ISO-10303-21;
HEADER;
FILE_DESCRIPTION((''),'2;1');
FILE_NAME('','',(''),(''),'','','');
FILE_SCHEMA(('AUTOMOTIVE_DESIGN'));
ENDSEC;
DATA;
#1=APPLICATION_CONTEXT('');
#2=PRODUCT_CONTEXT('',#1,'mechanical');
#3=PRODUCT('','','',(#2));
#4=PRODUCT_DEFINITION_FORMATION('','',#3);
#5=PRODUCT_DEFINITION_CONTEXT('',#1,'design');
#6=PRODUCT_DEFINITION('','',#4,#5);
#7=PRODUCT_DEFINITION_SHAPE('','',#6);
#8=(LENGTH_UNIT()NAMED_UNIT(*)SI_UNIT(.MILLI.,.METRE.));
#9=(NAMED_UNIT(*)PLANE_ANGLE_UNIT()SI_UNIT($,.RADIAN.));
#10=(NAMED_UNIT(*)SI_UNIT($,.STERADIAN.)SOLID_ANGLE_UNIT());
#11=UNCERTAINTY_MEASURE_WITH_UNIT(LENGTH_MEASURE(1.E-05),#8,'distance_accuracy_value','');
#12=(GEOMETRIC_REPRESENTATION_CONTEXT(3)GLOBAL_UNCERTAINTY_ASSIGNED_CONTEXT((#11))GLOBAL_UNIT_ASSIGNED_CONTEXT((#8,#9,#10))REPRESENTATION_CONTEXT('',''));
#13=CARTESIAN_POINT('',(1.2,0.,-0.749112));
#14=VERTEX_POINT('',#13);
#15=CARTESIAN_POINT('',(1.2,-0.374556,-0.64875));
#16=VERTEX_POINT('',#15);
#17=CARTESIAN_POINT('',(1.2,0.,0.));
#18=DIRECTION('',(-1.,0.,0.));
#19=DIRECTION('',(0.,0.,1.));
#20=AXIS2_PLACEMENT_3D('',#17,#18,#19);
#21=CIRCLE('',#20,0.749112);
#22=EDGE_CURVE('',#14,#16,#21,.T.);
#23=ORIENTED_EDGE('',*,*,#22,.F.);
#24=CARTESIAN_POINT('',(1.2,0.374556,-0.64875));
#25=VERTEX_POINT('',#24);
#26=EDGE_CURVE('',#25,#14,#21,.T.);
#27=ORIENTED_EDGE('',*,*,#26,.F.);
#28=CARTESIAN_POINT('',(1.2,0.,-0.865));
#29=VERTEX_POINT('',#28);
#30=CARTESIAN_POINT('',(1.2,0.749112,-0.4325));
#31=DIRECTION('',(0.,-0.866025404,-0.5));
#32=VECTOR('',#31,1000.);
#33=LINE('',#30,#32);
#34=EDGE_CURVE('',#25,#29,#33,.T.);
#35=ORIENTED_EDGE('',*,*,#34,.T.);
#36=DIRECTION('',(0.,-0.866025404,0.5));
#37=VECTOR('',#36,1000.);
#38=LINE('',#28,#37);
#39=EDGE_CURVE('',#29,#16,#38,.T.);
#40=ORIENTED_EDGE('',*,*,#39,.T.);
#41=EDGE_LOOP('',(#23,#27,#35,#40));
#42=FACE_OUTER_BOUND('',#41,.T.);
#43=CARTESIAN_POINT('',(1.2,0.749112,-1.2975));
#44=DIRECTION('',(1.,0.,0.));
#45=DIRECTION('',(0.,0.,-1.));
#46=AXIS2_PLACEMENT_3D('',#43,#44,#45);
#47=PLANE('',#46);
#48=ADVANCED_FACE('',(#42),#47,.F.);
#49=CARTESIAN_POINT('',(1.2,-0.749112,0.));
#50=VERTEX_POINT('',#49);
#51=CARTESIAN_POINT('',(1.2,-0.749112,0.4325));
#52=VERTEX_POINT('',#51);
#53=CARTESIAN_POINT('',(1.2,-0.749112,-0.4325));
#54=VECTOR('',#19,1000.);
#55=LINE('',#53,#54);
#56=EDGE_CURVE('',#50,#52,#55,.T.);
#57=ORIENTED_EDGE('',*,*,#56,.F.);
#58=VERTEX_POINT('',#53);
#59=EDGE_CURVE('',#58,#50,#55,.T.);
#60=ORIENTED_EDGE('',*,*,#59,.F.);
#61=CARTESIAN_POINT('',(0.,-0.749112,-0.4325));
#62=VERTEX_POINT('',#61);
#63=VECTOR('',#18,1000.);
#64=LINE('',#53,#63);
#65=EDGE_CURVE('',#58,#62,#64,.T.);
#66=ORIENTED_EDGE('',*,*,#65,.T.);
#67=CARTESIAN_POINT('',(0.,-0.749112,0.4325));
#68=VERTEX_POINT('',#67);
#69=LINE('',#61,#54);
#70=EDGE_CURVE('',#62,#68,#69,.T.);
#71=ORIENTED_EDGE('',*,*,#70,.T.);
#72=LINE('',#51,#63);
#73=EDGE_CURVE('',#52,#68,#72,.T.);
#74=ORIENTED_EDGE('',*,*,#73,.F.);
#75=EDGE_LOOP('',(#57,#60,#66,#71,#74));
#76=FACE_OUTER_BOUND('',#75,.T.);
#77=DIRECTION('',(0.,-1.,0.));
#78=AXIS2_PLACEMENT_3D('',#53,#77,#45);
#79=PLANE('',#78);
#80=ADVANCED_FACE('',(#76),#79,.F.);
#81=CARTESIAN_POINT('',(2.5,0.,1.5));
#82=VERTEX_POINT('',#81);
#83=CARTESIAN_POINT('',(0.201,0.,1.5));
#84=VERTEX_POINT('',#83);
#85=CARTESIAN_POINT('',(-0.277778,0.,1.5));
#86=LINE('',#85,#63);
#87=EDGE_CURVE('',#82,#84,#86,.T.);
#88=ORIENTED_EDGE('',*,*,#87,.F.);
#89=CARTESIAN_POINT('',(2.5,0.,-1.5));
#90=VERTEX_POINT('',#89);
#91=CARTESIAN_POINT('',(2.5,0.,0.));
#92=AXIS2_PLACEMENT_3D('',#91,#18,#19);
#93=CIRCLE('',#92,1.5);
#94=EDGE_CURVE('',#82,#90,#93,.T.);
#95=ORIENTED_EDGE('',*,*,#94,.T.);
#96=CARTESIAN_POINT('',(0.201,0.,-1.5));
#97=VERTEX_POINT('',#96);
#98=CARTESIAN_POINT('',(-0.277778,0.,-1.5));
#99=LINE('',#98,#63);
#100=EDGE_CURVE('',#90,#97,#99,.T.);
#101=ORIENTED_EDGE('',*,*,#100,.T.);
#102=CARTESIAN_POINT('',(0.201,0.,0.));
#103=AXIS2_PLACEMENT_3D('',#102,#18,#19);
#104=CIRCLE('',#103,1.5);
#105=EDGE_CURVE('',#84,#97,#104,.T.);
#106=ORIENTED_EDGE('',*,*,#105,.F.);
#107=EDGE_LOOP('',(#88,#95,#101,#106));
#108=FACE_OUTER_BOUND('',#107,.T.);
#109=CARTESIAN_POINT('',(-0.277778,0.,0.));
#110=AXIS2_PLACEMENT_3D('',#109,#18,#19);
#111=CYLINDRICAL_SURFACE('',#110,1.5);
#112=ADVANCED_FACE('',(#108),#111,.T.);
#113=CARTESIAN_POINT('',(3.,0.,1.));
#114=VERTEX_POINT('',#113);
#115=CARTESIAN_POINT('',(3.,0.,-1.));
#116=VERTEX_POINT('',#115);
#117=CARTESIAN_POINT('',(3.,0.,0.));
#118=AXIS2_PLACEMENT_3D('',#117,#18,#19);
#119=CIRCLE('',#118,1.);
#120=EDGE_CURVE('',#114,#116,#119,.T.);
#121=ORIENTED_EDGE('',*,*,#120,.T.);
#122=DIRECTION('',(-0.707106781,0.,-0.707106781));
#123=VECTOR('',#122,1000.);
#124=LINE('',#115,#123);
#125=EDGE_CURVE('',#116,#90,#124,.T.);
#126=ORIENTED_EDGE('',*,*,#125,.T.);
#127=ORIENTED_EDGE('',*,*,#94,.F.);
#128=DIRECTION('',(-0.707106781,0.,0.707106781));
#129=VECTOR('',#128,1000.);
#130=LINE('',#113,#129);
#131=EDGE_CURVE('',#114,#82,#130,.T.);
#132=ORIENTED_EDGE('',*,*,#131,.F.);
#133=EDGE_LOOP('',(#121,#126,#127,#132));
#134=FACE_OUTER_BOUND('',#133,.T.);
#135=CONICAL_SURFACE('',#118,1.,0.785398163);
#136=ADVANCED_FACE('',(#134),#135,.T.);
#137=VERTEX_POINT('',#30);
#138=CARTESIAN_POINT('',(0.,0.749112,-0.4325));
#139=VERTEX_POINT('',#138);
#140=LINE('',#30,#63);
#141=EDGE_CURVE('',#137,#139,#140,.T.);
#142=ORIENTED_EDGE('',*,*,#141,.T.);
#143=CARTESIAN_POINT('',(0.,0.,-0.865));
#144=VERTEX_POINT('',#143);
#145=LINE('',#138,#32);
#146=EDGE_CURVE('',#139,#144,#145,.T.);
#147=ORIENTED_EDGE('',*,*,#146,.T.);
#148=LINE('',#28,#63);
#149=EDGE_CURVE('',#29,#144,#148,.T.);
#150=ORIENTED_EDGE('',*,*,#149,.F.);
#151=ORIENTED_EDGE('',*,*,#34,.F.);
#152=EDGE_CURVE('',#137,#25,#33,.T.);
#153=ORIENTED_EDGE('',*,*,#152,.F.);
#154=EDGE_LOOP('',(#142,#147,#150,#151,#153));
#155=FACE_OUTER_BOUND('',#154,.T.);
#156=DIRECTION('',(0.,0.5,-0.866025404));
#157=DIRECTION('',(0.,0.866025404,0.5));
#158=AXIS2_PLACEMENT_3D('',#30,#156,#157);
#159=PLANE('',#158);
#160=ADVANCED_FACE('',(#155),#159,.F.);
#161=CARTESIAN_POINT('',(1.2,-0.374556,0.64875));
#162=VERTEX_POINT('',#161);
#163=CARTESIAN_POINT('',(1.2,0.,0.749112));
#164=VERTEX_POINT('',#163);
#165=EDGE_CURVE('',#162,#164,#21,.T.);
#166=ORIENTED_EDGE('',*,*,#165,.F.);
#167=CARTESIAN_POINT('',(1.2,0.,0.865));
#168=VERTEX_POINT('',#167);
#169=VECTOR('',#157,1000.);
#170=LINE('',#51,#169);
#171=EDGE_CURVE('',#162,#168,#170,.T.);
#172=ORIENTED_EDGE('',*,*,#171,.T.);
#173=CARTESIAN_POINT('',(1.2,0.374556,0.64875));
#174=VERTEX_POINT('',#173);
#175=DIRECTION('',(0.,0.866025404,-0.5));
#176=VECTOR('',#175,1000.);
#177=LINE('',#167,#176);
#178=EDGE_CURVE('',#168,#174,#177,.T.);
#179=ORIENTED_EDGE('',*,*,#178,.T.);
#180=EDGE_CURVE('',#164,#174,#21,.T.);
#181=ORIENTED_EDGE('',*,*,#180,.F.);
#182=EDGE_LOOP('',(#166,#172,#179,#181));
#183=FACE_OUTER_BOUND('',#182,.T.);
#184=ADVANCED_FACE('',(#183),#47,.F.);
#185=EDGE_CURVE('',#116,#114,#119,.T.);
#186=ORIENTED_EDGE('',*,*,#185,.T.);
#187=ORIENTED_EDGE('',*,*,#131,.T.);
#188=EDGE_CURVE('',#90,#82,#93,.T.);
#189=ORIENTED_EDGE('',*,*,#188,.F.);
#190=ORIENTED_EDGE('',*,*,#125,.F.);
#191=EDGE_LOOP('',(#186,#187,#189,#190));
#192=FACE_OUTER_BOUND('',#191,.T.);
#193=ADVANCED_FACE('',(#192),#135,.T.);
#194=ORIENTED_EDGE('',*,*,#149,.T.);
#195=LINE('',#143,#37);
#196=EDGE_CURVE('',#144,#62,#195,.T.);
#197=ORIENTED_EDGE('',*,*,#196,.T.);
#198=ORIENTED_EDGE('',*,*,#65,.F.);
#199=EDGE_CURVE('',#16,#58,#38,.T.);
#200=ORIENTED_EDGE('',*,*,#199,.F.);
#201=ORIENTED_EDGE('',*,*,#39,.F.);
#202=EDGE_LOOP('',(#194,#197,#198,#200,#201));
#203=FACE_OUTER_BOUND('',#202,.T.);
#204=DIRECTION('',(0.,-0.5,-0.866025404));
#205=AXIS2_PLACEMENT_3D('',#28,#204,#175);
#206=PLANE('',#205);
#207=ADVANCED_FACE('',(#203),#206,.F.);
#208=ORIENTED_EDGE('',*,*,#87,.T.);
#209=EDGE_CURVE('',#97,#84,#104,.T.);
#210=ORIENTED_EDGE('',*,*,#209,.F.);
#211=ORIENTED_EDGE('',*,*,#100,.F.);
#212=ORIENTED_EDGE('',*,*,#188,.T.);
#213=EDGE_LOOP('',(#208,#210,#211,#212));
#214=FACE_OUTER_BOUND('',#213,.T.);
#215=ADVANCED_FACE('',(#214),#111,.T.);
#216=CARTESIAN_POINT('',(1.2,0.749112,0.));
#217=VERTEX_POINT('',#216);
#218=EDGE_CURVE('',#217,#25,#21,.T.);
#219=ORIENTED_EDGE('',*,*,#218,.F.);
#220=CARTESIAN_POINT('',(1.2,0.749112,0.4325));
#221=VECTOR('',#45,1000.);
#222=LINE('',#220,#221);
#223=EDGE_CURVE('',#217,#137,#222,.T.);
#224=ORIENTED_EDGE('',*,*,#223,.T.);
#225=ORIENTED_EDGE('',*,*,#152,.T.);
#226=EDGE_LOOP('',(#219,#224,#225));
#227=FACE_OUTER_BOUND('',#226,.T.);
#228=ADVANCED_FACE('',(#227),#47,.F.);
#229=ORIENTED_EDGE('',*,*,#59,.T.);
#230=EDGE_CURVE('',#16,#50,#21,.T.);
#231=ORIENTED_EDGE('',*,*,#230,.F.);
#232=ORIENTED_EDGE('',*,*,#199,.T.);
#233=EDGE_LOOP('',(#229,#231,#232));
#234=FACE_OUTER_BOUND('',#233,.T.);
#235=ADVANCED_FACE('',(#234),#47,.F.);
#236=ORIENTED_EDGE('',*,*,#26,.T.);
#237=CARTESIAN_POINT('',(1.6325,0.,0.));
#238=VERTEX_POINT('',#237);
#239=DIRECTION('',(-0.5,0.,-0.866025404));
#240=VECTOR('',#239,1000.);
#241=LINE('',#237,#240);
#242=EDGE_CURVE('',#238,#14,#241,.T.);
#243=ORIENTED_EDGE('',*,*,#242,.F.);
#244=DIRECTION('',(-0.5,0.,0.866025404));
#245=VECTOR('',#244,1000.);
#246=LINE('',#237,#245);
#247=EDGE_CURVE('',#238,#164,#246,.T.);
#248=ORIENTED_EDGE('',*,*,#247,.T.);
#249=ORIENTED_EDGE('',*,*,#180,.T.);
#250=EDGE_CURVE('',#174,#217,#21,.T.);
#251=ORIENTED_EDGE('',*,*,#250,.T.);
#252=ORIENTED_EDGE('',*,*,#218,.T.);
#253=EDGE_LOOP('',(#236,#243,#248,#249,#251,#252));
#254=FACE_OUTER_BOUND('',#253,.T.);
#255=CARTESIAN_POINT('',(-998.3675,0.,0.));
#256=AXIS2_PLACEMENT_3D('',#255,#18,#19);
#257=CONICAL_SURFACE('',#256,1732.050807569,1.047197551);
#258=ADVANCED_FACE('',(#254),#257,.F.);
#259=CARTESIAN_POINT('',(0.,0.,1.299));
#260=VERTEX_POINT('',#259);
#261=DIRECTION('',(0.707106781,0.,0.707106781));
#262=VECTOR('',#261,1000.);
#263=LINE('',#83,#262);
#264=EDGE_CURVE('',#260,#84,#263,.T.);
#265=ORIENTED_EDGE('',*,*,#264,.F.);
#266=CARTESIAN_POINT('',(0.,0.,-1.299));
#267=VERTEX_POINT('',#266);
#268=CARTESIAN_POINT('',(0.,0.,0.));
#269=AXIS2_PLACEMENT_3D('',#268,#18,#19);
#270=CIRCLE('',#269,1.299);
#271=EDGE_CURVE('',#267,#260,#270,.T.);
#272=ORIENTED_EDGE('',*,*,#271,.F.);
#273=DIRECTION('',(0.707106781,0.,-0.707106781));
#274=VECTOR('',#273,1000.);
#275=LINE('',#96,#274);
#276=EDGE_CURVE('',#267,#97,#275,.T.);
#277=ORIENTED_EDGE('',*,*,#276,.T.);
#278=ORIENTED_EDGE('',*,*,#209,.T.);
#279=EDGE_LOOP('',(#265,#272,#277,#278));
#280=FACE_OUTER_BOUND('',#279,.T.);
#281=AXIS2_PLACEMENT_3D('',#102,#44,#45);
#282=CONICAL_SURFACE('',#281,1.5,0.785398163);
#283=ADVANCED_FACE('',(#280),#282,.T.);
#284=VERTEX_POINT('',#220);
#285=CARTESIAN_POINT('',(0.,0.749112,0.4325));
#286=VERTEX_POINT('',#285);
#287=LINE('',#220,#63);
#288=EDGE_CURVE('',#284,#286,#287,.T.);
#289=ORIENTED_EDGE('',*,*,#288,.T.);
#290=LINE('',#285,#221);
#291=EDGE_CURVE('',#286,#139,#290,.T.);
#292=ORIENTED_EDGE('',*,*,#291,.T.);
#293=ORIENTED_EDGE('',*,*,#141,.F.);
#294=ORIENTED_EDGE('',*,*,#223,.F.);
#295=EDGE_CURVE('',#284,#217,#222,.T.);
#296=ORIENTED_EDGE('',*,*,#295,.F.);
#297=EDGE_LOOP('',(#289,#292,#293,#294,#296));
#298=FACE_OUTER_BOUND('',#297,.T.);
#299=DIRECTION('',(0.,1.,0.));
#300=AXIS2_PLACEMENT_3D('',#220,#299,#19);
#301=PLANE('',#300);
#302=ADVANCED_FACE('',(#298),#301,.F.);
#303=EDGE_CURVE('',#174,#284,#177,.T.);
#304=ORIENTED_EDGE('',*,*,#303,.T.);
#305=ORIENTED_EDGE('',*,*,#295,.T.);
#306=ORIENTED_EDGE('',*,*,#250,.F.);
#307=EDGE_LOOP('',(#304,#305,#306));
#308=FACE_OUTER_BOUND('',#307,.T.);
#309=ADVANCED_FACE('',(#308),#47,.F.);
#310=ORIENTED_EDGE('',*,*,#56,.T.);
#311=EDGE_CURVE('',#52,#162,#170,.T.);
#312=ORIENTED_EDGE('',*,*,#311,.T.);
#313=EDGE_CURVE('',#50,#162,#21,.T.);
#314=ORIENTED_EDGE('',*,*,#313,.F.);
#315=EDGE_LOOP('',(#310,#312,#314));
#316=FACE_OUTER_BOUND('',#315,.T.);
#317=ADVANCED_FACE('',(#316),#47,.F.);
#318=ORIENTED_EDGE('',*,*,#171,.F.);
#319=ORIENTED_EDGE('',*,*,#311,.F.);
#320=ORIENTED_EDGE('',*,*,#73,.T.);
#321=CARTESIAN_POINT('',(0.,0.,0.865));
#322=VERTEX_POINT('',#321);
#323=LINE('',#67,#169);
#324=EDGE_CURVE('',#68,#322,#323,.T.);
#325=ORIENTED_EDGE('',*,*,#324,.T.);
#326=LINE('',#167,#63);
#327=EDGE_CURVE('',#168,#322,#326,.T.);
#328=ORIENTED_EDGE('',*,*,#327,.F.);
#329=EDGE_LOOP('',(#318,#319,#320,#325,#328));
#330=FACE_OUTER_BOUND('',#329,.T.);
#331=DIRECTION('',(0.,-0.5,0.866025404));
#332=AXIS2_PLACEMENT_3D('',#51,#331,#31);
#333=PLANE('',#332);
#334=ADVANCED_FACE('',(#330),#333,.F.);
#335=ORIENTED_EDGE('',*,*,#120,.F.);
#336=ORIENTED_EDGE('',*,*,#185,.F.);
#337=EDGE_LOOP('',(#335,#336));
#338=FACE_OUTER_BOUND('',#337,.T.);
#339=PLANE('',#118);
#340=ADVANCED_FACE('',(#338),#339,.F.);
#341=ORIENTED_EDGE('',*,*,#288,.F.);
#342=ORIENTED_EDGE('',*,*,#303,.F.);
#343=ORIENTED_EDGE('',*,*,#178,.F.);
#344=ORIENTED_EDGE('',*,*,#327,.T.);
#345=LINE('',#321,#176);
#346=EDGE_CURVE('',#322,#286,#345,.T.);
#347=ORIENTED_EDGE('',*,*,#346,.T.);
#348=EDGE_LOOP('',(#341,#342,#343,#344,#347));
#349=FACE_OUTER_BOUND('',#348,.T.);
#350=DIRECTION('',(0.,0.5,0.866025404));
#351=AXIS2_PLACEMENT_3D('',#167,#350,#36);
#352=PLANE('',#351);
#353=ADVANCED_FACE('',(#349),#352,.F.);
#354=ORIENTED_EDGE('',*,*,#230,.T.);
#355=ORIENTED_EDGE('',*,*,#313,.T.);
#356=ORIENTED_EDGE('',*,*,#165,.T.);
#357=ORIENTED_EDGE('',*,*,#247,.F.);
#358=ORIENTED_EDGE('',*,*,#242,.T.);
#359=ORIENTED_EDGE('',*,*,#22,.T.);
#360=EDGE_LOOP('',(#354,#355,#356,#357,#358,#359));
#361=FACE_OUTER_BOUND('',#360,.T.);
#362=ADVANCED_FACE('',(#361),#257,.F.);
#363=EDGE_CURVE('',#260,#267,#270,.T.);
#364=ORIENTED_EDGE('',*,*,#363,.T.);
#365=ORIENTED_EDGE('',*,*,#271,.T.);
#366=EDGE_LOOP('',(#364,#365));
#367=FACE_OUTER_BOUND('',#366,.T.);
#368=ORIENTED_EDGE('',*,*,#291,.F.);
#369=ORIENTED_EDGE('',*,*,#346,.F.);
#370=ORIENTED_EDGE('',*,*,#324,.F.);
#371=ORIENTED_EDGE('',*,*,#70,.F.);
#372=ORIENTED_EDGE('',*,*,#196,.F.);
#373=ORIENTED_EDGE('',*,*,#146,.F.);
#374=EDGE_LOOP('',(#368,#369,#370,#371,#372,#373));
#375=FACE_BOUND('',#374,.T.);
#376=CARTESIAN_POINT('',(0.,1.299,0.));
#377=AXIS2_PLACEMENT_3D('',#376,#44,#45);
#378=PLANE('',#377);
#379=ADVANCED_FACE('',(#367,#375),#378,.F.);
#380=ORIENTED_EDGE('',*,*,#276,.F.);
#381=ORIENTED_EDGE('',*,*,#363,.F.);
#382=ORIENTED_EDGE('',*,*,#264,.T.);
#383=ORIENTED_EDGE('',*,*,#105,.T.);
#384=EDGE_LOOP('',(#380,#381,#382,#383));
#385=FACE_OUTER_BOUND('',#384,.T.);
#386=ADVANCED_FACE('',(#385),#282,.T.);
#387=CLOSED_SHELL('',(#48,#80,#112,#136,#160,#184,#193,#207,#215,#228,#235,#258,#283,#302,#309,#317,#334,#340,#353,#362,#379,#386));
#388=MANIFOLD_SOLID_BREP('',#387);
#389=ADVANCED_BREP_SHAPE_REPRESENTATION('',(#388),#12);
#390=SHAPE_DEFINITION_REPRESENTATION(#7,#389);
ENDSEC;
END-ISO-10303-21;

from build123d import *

# Parameters (mm, degrees)
CUT_EXTRUDE1_DEPTH = 1.2


with BuildPart() as part:
    # Sketch1 → Base-Revolve (revolve)
    with BuildSketch(Plane.XY, mode=Mode.PRIVATE) as base_revolve_sk:
        Polygon((0, 0), (3, 0), (3, 1), (2.5, 1.5), (0.201, 1.5), (0, 1.299), align=None)
    revolve(base_revolve_sk.sketch.rotate(Axis((-0.277777778, 0, 0), (1, 0, 0)), 90), axis=Axis((-0.277777778, 0, 0), (1, 0, 0)))

    # Sketch2 → Cut-Extrude1 (cut)
    with BuildSketch(Plane.ZY):
        Polygon((-0.4325, -0.749111974), (0.4325, -0.749111974), (0.865, 0), (0.4325, 0.749111974), (-0.4325, 0.749111974), (-0.865, 0), align=None)
    extrude(amount=-CUT_EXTRUDE1_DEPTH, mode=Mode.SUBTRACT)

    # Sketch4 → Cut-Revolve2 (revolve, cut)
    with BuildSketch(Plane.XY, mode=Mode.PRIVATE) as cut_revolve2_sk:
        Polygon((1.2, 0.749111974), (1.6325, 0), (1.2, 0), align=None)
    revolve(cut_revolve2_sk.sketch.rotate(Axis((-0.277777778, 0, 0), (1, 0, 0)), 90), axis=Axis((-0.277777778, 0, 0), (1, 0, 0)), mode=Mode.SUBTRACT)


solid = part.part
